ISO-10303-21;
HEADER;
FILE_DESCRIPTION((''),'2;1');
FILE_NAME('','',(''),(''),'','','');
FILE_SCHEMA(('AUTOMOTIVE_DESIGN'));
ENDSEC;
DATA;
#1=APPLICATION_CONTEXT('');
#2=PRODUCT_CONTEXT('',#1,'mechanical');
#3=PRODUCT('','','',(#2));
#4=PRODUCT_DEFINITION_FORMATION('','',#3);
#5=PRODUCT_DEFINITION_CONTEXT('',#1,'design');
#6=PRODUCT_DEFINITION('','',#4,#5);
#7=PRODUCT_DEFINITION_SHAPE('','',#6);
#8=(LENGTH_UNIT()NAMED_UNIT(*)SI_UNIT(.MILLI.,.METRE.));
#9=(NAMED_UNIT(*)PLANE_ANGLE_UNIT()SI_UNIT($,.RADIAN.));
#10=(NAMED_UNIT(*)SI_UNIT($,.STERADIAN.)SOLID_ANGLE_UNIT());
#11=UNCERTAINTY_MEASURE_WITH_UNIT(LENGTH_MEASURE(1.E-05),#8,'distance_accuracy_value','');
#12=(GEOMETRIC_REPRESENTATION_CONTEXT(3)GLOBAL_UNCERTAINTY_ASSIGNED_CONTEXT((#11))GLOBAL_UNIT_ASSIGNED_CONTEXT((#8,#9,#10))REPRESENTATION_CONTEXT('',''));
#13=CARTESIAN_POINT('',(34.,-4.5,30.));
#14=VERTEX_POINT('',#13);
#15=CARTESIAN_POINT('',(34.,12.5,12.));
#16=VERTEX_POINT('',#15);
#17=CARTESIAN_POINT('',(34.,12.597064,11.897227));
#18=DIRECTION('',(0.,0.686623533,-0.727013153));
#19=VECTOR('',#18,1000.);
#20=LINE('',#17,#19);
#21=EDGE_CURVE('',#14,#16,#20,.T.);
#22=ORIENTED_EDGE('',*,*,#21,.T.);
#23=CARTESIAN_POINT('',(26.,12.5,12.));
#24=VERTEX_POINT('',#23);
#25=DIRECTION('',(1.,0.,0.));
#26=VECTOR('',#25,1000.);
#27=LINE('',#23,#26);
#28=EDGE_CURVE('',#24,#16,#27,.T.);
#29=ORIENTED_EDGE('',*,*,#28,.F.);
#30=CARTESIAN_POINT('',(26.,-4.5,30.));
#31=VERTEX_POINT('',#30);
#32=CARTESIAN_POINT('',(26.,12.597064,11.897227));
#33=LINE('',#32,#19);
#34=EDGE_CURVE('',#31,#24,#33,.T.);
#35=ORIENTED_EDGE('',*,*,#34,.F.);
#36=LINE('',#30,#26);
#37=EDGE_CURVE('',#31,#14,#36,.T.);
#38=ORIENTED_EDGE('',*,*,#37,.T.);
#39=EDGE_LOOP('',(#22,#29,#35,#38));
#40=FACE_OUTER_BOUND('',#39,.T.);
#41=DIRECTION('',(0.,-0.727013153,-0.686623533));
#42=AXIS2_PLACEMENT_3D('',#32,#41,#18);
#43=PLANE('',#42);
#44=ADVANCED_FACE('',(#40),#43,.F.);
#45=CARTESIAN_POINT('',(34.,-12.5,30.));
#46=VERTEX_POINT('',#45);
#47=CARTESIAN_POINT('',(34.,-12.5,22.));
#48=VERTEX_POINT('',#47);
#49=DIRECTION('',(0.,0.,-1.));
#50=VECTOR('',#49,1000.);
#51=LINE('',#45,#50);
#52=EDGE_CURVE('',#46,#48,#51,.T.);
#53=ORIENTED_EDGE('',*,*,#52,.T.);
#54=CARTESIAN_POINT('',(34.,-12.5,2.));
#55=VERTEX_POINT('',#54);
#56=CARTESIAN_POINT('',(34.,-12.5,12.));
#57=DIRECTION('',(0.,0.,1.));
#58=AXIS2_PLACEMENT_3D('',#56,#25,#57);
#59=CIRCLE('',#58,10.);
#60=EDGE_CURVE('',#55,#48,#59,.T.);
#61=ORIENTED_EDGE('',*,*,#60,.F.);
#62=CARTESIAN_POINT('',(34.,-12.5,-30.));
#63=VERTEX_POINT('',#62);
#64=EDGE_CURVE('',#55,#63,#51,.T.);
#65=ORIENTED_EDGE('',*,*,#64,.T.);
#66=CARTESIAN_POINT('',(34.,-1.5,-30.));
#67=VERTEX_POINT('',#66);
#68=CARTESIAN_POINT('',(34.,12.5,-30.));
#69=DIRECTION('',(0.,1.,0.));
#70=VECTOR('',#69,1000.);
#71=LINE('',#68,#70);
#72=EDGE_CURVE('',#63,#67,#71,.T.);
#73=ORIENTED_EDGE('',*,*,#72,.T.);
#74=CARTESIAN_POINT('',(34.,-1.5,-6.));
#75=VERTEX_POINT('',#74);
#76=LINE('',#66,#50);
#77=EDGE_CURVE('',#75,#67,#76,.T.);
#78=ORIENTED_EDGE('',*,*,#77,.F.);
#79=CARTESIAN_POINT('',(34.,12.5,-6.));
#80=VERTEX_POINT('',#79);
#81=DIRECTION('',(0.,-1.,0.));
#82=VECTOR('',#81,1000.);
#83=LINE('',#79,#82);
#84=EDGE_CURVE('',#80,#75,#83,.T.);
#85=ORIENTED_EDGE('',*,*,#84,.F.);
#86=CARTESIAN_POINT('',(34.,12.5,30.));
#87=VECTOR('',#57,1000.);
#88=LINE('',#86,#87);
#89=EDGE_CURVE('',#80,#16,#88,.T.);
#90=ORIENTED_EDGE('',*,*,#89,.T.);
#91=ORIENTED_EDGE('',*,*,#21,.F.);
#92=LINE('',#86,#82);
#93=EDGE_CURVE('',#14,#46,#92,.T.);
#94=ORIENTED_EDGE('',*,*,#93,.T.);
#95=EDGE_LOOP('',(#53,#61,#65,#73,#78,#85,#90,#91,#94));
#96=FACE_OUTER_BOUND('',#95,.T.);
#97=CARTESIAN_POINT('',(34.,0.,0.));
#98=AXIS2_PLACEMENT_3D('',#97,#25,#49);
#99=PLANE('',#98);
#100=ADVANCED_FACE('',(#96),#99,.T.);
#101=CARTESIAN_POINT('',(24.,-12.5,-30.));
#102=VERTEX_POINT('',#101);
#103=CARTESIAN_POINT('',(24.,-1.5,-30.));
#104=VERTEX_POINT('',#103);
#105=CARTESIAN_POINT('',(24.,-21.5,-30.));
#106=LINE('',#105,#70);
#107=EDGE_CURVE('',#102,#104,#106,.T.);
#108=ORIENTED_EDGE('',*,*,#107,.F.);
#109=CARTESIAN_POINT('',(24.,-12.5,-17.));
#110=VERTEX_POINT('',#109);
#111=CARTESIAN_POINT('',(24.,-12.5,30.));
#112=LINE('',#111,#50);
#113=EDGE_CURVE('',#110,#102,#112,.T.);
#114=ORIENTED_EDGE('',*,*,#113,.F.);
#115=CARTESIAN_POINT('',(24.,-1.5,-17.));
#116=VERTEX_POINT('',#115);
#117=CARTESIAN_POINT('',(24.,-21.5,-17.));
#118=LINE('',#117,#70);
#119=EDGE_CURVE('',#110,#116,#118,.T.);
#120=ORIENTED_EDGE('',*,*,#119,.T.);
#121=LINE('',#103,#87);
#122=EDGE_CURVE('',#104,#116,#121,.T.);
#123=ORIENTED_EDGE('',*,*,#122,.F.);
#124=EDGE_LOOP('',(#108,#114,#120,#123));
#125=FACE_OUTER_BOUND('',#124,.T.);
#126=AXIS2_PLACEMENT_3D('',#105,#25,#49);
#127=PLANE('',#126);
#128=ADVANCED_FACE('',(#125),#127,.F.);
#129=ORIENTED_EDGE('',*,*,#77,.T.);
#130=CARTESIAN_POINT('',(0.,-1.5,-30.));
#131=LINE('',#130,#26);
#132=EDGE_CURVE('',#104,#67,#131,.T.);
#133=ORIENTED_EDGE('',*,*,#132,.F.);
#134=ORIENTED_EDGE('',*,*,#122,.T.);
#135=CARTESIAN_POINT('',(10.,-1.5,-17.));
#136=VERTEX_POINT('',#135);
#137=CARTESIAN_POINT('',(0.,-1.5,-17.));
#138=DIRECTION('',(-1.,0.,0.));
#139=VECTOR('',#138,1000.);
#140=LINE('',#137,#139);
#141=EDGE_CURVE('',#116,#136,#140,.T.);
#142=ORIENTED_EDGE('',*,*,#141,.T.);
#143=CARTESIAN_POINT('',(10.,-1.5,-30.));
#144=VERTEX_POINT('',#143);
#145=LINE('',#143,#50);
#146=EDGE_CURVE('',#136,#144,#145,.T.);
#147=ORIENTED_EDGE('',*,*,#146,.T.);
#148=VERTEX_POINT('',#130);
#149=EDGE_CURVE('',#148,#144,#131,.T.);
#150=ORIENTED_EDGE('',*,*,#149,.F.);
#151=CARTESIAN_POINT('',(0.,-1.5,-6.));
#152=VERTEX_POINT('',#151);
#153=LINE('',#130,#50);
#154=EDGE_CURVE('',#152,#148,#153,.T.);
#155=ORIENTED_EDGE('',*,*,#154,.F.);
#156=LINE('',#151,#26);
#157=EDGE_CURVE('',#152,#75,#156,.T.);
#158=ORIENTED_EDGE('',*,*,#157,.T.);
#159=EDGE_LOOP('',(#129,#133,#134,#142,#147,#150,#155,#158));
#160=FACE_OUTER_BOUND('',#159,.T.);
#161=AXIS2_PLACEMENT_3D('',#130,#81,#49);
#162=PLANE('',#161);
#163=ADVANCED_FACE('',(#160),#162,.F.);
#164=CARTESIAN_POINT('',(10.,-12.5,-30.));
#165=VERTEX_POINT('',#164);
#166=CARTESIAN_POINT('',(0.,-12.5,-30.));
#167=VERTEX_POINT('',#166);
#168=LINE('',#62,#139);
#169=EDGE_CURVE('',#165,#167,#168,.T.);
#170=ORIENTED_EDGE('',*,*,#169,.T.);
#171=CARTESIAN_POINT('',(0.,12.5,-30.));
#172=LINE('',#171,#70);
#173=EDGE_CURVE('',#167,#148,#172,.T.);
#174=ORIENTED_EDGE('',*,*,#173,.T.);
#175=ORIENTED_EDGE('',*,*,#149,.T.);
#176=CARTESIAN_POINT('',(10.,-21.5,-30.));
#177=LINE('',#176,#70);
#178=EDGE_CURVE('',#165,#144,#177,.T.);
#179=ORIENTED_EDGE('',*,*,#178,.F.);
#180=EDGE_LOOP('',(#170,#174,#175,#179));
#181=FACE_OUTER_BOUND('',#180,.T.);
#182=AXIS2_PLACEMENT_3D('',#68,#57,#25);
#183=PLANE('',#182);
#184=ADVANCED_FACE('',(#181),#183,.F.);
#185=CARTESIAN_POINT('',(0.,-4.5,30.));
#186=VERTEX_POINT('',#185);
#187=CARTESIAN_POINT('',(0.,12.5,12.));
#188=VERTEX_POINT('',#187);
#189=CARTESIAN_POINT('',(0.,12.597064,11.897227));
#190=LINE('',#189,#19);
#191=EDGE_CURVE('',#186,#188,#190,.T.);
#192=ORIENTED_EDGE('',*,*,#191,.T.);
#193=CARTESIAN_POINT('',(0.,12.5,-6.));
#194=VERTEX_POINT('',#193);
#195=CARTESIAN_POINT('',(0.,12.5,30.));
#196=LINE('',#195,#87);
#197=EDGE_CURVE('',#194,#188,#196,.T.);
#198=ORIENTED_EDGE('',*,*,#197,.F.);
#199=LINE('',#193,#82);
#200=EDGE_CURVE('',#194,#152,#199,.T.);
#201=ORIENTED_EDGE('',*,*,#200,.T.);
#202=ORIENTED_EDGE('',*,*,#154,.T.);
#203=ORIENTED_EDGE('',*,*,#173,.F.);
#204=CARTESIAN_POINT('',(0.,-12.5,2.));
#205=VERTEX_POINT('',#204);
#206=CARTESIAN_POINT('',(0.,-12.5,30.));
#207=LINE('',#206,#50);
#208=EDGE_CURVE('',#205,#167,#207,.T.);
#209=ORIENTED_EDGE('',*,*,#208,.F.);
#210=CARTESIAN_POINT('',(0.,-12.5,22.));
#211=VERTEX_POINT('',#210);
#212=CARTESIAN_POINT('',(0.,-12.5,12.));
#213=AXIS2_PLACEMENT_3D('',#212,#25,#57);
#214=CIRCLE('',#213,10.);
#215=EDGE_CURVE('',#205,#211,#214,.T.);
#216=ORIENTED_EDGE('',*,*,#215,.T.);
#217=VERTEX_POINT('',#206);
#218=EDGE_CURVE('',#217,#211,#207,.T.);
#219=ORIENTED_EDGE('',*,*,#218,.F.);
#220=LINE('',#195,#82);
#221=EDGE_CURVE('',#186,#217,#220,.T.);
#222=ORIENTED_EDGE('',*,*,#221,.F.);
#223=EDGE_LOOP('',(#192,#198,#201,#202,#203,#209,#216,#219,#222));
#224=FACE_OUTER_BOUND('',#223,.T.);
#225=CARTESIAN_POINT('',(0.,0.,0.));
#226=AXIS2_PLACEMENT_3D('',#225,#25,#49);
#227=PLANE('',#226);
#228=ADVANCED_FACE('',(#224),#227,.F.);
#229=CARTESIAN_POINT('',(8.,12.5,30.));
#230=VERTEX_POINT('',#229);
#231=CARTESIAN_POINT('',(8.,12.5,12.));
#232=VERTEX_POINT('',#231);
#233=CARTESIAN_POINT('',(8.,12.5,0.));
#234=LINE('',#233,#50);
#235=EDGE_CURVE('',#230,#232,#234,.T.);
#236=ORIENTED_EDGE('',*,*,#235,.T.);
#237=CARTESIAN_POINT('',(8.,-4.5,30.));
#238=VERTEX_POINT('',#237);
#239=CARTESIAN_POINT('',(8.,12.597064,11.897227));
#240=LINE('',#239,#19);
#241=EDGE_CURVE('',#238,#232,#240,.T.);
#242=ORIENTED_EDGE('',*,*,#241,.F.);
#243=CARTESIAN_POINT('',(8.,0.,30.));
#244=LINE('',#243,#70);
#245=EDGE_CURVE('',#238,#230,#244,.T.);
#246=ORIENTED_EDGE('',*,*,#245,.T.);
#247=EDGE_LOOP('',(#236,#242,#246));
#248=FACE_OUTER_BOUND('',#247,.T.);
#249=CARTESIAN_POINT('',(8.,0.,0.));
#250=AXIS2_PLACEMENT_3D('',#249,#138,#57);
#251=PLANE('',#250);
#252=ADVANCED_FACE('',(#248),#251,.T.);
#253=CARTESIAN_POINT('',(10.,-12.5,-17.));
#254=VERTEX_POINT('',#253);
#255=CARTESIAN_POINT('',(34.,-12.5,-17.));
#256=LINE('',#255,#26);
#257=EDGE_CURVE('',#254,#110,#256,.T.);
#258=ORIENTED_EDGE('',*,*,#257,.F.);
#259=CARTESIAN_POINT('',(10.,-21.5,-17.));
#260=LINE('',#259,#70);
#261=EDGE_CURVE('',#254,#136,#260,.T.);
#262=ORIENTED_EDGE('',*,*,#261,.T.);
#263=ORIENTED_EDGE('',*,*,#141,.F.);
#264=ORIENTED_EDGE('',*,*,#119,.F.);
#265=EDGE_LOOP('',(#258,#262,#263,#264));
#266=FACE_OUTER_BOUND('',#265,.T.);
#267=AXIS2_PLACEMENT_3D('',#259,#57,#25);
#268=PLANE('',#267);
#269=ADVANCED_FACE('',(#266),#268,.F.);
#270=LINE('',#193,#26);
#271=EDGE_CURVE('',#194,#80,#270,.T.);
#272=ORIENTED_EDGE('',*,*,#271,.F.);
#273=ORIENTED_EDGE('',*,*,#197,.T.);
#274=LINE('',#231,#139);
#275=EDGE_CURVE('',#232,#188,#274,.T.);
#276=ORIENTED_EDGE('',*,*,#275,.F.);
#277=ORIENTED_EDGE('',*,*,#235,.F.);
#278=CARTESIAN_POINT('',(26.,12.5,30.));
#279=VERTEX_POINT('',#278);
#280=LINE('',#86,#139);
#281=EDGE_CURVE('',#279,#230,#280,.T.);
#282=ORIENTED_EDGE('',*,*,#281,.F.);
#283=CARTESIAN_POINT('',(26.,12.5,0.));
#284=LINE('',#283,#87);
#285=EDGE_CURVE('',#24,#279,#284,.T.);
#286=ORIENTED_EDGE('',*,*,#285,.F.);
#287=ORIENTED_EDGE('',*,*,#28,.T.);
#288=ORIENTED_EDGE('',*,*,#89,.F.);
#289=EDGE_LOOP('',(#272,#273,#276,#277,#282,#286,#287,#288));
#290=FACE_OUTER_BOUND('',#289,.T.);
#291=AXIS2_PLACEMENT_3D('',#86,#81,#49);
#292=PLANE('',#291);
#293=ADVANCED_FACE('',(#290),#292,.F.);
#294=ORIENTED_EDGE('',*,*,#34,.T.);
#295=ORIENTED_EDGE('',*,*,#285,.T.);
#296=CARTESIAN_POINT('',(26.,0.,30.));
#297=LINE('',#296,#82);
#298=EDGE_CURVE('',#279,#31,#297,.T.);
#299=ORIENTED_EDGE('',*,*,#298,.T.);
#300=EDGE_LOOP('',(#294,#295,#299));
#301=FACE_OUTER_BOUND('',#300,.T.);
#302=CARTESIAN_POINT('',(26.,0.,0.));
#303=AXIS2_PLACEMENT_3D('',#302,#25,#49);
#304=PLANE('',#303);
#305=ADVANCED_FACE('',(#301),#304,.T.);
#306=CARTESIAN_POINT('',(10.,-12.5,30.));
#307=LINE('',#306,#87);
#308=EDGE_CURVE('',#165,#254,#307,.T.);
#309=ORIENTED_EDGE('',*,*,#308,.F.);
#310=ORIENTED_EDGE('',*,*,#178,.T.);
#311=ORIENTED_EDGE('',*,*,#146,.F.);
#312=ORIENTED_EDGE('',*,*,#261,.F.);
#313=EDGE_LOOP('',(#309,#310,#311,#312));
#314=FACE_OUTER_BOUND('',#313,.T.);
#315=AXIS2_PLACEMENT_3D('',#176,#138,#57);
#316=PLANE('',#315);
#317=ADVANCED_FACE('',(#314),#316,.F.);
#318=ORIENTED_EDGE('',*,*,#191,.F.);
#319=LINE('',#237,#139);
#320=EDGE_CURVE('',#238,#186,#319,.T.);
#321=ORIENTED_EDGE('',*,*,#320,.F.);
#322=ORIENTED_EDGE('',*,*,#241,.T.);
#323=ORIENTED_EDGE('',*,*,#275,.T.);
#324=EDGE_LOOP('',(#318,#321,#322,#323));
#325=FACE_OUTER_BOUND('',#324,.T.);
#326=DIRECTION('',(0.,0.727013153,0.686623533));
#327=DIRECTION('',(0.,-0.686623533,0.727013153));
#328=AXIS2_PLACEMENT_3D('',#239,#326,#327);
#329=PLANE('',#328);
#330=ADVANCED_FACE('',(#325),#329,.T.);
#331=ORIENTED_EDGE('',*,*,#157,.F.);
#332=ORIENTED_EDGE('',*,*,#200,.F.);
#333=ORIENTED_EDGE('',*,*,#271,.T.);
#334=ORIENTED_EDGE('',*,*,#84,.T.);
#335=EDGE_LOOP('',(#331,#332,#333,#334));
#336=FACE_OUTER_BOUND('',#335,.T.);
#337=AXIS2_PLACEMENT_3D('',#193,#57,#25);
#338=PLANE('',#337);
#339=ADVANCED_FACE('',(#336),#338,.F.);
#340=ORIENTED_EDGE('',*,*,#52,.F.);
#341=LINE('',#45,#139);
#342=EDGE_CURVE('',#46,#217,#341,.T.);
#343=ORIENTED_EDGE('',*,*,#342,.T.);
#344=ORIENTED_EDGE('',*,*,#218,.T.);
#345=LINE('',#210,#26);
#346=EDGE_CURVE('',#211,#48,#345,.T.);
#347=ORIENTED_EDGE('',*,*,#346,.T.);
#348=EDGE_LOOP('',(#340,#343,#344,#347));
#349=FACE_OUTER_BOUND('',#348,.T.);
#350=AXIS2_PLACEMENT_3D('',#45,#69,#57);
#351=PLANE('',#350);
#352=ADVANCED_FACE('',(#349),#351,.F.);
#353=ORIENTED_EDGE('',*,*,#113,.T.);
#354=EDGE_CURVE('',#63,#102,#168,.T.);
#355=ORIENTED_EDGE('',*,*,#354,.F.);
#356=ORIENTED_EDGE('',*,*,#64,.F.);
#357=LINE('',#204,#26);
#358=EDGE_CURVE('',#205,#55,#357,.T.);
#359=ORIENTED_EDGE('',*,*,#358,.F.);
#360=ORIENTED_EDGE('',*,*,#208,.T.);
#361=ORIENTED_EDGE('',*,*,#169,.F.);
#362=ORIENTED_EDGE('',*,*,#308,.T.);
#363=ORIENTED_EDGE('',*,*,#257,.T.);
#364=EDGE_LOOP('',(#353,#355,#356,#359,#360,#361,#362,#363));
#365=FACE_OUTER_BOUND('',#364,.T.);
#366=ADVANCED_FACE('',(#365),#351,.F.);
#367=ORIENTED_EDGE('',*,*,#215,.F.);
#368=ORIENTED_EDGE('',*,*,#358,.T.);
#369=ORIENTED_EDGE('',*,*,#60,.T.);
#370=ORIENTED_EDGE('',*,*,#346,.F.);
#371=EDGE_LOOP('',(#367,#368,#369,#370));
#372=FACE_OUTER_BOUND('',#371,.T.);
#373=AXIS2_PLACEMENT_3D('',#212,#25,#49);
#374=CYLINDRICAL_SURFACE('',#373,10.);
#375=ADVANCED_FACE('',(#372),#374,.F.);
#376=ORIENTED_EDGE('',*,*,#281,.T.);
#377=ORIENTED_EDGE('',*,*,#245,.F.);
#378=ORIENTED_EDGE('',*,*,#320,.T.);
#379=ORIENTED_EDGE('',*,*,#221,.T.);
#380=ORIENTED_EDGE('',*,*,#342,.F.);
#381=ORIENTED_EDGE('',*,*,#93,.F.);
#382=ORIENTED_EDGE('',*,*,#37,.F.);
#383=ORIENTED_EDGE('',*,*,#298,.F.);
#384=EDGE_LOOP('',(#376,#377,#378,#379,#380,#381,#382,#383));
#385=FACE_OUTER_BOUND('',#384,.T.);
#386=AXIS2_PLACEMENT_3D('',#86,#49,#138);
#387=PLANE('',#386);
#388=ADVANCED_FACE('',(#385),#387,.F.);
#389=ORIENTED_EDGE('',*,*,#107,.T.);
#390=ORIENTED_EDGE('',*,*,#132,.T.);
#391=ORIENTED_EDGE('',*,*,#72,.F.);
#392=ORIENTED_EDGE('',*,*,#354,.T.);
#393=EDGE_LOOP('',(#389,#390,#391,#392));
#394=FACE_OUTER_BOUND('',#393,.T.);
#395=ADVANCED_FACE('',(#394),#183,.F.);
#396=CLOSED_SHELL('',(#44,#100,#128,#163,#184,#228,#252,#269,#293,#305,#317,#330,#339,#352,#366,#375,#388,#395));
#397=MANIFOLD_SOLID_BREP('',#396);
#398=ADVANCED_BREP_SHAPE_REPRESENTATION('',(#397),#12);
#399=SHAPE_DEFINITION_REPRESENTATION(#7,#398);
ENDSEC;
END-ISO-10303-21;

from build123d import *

# Parameters (mm, degrees)
BLOCK_PROFILE_SKETCH_W       = 60
BLOCK_PROFILE_SKETCH_H       = 25
BASE_BLOCK_DEPTH             = 34
STEP_CUT_PROFILE_SKETCH_W    = 24
STEP_CUT_PROFILE_SKETCH_H    = 14
STEPPED_THROUGH_CUT_DEPTH    = 34
NOTCH_PROFILE_SKETCH_W       = 14
NOTCH_PROFILE_SKETCH_H       = 13
SIDE_NOTCH_THROUGH_CUT_DEPTH = 34
SLOT_18X8_DEPTH_8_DEPTH      = 8
ARCH_RELIEF_CUT_DEPTH        = 8


with BuildPart() as part:
    # Block Profile Sketch → Base Block (new body)
    with BuildSketch(Plane(origin=(0, 0, 0), x_dir=(0, 0, -1), z_dir=(1, 0, 0))):
        Rectangle(BLOCK_PROFILE_SKETCH_W, BLOCK_PROFILE_SKETCH_H)
    extrude(amount=BASE_BLOCK_DEPTH)

    # Step Cut Profile Sketch → Stepped Through Cut (cut)
    with BuildSketch(Plane(origin=(34, 0, 0), x_dir=(0, 0, -1), z_dir=(1, 0, 0))):
        with Locations((18, 5.5)):
            Rectangle(STEP_CUT_PROFILE_SKETCH_W, STEP_CUT_PROFILE_SKETCH_H)
        with BuildLine():
            Line((-22, -12.5), (-2, -12.5))
            ThreePointArc((-2, -12.5), (-12, -2.5), (-22, -12.5))
        make_face()
    extrude(amount=-STEPPED_THROUGH_CUT_DEPTH, mode=Mode.SUBTRACT)

    # Notch Profile Sketch → Side Notch Through Cut (cut)
    with BuildSketch(Plane(origin=(0, 12.5, 0), x_dir=(1, 0, 0), z_dir=(0, 1, 0))):
        with Locations((17, 23.5)):
            Rectangle(NOTCH_PROFILE_SKETCH_W, NOTCH_PROFILE_SKETCH_H)
    extrude(amount=-SIDE_NOTCH_THROUGH_CUT_DEPTH, mode=Mode.SUBTRACT)

    # Slot Sketch → Slot 18x8 Depth 8 (cut)
    with BuildSketch(Plane(origin=(34, 0, 0), x_dir=(0, 0, -1), z_dir=(1, 0, 0))):
        Polygon((-30, 12.5), (-30, -4.5), (-12, 12.5), align=None)
    extrude(amount=-SLOT_18X8_DEPTH_8_DEPTH, mode=Mode.SUBTRACT)

    # Arch Relief Sketch → Arch Relief Cut (cut)
    with BuildSketch(Plane.ZY):
        Polygon((12, 12.5), (30, -4.5), (30, 12.5), align=None)
    extrude(amount=-ARCH_RELIEF_CUT_DEPTH, mode=Mode.SUBTRACT)


solid = part.part
